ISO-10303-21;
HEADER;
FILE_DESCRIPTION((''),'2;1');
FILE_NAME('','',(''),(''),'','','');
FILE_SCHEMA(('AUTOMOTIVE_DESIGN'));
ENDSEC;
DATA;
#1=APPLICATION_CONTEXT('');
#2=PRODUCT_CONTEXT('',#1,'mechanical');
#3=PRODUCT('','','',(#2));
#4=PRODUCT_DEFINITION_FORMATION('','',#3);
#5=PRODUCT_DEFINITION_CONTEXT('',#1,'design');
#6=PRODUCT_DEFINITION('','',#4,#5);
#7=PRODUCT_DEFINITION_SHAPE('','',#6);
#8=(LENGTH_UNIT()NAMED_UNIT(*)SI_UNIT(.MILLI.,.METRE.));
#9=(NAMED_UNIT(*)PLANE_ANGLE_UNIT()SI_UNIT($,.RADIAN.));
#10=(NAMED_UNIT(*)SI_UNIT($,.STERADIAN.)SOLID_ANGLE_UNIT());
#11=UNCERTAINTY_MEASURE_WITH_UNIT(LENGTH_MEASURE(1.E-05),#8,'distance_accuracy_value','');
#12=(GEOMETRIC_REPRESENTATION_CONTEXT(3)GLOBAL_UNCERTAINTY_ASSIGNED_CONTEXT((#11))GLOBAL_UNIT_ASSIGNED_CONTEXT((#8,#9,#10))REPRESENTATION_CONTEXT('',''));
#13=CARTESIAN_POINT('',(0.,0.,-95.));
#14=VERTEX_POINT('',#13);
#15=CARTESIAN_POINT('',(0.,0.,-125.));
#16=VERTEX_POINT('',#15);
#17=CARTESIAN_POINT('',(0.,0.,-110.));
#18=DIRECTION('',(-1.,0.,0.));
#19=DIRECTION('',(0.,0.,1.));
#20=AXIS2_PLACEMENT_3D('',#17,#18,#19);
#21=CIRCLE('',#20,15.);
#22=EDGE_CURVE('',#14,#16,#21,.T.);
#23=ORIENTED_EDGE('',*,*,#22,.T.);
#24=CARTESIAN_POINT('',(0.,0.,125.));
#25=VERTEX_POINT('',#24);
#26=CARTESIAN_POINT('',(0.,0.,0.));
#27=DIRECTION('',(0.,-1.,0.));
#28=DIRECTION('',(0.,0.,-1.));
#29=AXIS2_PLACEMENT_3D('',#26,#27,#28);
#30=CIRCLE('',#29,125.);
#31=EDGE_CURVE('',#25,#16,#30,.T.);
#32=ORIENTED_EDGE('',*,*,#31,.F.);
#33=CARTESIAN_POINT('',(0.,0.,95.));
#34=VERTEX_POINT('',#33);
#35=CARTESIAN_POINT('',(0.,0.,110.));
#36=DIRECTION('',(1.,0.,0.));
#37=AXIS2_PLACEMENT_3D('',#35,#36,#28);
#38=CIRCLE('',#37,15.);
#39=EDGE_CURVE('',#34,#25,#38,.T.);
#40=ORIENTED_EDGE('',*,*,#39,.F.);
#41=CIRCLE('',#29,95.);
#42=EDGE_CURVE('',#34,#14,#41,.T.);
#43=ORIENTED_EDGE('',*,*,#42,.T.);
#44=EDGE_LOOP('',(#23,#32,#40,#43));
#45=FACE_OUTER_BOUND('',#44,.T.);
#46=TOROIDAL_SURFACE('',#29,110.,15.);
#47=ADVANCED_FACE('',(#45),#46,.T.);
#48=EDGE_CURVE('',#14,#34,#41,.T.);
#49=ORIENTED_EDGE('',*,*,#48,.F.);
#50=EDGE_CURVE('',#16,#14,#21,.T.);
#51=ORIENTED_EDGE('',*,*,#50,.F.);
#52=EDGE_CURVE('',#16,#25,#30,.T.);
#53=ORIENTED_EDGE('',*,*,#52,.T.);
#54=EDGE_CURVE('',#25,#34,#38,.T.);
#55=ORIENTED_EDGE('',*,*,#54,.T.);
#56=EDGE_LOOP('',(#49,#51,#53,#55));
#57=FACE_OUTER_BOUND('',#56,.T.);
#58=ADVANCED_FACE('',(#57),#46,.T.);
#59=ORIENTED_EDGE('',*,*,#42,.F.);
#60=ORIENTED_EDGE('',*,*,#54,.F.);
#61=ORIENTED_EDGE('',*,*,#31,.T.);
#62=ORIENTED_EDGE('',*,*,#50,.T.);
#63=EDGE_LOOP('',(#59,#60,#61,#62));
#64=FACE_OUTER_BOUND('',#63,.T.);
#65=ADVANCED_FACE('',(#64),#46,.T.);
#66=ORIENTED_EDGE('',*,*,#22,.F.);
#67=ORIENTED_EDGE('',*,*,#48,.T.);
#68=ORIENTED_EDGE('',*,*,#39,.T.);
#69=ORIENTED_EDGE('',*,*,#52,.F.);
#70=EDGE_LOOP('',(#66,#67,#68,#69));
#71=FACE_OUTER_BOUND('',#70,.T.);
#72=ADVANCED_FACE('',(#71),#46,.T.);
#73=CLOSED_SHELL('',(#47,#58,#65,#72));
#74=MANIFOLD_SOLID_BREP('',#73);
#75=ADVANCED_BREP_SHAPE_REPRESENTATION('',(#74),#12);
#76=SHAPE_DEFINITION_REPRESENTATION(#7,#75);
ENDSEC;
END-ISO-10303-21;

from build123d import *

# Parameters (mm, degrees)
SKETCH1_R = 15


with BuildPart() as part:
    # Sketch1 → Revolve1 (revolve)
    with BuildSketch(Plane.XY, mode=Mode.PRIVATE) as revolve1_sk:
        with Locations((110, 0)):
            Circle(SKETCH1_R)
    revolve(revolve1_sk.sketch.rotate(Axis((0, 0, 0), (0, 1, 0)), 90), axis=Axis((0, 0, 0), (0, 1, 0)))


solid = part.part
